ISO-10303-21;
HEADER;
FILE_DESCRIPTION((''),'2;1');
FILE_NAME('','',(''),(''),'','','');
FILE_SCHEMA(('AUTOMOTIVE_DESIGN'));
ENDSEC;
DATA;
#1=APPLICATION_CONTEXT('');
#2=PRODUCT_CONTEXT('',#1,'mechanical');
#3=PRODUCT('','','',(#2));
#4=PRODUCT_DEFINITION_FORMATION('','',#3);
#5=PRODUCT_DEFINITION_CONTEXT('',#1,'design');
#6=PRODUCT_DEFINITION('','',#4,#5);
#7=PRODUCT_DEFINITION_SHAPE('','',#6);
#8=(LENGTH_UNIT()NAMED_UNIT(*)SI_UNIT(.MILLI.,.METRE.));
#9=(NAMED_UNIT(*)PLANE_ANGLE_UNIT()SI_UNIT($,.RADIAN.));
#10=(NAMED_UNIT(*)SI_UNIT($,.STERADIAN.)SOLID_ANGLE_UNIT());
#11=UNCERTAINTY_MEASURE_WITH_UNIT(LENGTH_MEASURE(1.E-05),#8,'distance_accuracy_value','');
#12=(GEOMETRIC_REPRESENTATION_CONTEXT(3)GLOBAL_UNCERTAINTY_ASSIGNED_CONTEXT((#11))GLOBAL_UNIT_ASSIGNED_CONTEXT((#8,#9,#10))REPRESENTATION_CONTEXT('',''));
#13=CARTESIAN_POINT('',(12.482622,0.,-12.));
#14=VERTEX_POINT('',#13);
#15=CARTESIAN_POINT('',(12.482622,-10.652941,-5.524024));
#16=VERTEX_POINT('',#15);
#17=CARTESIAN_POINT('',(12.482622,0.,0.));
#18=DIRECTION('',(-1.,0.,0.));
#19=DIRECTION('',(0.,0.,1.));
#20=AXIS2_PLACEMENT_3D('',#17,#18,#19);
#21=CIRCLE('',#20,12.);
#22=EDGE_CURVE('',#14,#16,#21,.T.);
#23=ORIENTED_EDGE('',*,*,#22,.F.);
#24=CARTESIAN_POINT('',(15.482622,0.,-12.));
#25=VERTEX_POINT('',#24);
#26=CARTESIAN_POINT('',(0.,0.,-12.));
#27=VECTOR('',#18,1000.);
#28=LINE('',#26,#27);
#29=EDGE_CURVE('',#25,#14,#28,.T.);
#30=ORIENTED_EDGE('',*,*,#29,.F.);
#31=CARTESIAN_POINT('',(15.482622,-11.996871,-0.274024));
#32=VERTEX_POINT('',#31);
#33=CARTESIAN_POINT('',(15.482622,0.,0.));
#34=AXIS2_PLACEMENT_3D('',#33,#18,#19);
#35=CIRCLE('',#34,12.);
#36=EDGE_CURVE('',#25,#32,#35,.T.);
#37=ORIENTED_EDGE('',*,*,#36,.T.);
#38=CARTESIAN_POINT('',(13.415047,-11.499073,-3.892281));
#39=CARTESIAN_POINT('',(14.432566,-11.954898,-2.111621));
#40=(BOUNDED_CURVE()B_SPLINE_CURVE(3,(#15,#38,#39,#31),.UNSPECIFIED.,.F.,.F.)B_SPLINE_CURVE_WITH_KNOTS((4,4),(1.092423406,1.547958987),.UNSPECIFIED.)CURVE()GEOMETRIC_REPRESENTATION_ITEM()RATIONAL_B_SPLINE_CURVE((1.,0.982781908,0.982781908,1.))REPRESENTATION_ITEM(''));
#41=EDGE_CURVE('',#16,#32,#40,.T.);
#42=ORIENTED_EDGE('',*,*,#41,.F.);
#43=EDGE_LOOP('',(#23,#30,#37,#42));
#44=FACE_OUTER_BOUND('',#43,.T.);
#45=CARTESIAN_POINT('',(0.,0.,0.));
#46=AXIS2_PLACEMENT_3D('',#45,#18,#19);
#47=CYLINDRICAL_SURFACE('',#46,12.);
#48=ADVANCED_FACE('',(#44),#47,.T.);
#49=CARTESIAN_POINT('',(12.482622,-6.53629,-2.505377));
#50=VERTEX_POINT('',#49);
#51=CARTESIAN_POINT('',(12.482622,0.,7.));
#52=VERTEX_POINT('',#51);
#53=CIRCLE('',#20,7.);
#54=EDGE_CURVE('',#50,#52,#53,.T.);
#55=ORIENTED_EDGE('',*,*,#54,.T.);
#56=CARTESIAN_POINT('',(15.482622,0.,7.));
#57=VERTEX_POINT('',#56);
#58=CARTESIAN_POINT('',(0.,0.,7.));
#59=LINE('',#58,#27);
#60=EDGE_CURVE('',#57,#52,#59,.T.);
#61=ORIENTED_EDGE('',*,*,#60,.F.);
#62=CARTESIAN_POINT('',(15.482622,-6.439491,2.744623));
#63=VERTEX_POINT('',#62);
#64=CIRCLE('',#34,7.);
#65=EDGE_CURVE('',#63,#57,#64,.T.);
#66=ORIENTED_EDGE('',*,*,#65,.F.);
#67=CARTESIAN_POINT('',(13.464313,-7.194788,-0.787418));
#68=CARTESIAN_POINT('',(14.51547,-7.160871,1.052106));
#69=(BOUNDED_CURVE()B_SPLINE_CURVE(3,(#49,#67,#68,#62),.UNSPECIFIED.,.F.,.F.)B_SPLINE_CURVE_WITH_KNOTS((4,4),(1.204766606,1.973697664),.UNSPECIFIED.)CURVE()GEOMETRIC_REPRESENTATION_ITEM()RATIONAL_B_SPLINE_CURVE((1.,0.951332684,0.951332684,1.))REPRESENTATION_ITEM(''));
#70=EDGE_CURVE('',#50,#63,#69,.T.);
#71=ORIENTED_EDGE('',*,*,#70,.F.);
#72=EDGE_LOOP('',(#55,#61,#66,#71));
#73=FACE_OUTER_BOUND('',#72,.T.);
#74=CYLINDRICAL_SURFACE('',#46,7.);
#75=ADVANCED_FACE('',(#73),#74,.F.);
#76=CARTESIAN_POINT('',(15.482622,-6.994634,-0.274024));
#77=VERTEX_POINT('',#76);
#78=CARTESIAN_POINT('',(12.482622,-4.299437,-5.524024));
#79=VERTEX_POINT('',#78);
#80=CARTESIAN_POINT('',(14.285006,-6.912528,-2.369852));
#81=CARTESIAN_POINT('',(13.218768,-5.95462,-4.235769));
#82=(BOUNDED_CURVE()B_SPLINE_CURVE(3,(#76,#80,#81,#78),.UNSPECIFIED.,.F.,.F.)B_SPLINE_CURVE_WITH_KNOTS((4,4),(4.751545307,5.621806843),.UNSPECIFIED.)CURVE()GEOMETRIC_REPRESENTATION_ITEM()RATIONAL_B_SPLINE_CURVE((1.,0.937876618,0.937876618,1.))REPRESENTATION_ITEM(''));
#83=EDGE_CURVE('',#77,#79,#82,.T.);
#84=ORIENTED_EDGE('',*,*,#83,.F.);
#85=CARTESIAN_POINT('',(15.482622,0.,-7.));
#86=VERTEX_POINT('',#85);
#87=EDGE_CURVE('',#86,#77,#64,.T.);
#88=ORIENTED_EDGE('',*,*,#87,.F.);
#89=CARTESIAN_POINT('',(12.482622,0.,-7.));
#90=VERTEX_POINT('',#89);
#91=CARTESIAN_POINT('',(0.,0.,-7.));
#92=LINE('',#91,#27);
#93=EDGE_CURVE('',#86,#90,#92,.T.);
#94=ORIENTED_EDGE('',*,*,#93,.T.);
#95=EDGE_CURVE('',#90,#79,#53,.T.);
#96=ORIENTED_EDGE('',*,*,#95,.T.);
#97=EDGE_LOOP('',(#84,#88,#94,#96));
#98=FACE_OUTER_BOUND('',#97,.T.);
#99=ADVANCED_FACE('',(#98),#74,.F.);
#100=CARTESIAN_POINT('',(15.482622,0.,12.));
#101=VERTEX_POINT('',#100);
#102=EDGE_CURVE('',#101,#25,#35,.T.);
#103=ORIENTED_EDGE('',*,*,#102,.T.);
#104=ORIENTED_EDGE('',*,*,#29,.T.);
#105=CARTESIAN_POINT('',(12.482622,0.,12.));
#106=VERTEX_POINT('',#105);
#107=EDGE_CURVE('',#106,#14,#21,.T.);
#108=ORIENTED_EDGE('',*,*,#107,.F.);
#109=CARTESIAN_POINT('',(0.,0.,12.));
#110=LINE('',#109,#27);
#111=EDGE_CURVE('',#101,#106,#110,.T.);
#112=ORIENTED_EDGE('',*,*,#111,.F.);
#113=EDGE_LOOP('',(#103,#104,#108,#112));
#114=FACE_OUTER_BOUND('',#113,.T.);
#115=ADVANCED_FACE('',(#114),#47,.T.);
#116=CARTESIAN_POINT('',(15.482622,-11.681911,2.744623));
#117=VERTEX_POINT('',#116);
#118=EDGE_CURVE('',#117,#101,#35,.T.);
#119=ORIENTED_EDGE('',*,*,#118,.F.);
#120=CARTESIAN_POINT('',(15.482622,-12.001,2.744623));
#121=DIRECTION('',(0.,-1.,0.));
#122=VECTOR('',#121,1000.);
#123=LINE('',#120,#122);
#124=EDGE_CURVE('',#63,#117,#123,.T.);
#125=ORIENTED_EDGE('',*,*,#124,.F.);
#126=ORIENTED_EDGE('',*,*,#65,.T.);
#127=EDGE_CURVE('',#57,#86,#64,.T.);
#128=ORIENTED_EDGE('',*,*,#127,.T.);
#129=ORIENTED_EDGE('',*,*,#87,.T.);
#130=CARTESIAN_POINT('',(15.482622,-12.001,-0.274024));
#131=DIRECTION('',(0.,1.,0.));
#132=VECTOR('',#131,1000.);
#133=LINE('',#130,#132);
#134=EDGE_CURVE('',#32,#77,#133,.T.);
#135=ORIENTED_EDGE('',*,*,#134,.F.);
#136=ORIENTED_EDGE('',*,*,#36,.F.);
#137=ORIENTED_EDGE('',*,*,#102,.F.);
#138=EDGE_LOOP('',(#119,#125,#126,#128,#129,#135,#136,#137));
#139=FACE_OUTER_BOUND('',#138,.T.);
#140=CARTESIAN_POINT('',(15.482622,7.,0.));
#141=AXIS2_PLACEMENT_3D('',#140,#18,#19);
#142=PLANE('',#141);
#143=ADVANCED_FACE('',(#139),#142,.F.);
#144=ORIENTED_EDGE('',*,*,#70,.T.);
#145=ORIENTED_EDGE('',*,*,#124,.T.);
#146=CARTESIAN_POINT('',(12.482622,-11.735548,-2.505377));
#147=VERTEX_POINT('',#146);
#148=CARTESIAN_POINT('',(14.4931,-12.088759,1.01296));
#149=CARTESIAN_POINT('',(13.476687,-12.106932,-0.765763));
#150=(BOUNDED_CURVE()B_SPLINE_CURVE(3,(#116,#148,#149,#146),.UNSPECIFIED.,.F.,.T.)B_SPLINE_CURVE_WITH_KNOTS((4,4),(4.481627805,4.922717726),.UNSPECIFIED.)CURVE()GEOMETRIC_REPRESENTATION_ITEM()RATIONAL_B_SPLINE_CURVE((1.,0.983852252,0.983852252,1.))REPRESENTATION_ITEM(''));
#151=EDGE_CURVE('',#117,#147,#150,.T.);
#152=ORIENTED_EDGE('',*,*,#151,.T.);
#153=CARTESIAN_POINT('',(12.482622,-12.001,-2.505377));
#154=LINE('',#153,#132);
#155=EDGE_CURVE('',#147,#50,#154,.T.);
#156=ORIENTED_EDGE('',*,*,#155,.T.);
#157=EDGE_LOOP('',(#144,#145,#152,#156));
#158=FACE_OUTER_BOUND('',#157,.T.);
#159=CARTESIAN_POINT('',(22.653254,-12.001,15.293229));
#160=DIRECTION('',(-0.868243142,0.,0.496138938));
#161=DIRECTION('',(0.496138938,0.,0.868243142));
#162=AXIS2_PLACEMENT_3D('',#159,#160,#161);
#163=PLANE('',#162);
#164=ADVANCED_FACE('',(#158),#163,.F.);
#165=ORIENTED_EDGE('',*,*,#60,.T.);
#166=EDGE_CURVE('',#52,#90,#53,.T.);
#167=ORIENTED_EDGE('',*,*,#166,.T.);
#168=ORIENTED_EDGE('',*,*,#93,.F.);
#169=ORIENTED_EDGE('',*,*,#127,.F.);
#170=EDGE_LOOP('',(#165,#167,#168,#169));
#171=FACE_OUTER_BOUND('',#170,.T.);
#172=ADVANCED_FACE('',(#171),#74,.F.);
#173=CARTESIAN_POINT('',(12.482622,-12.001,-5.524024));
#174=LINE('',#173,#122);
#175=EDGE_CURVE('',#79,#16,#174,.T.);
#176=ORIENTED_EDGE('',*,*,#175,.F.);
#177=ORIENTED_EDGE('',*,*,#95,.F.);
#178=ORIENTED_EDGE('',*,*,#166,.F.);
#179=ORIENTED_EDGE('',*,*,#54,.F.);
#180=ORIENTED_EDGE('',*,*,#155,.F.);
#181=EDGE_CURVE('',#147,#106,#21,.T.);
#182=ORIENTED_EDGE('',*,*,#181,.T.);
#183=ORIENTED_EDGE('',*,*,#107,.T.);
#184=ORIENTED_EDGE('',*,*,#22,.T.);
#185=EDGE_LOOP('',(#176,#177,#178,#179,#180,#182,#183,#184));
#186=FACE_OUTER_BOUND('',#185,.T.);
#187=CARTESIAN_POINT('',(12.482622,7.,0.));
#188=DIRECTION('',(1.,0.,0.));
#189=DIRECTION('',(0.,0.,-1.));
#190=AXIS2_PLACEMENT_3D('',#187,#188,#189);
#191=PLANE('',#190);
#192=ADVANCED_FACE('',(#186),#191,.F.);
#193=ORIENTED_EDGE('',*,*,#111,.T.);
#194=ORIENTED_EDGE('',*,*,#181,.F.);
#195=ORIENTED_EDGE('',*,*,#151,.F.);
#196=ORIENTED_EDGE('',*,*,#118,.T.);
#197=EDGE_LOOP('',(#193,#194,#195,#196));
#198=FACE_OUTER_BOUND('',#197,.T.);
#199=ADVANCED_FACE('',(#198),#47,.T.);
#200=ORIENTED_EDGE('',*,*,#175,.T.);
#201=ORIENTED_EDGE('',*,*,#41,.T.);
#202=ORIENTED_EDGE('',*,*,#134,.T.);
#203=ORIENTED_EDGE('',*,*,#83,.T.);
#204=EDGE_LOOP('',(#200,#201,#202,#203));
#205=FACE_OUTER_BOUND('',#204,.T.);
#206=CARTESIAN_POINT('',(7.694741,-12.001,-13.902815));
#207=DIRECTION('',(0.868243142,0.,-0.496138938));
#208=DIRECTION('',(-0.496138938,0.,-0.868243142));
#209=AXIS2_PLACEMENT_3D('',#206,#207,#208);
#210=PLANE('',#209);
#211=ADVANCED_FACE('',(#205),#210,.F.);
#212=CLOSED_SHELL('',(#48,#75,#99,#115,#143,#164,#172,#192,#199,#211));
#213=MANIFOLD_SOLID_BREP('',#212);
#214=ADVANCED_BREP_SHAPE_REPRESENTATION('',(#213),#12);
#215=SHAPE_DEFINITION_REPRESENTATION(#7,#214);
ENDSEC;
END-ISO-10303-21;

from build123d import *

# Parameters (mm, degrees)
SKETCH1_W          = 3
SKETCH1_H          = 5
CUT_EXTRUDE1_REACH = 24.972


with BuildPart() as part:
    # Sketch1 → Revolve1 (revolve)
    with BuildSketch(Plane.XY, mode=Mode.PRIVATE) as revolve1_sk:
        with Locations((13.982621868, 9.5)):
            Rectangle(SKETCH1_W, SKETCH1_H)
    revolve(revolve1_sk.sketch.rotate(Axis((0, 0, 0), (1, 0, 0)), 90), axis=Axis((0, 0, 0), (1, 0, 0)))

    # Sketch3 → Cut-Extrude1 (cut, up to next)
    with BuildSketch(Plane(origin=(0, 0, 0), x_dir=(1, 0, 0), z_dir=(0, 1, 0)), mode=Mode.PRIVATE) as cut_extrude1_sk1:
        Polygon((7.694741439, 13.902815003), (23.953594269, -14.55017745), (22.65325389, -15.293229095), (5.96980012, 13.902815003), align=None)
    cut_extrude1_tool1 = extrude(cut_extrude1_sk1.sketch, amount=-CUT_EXTRUDE1_REACH, mode=Mode.PRIVATE) & part.part
    add(cut_extrude1_tool1.solids().sort_by_distance((15.064598, 0, 0.510242))[0], mode=Mode.SUBTRACT)


solid = part.part
